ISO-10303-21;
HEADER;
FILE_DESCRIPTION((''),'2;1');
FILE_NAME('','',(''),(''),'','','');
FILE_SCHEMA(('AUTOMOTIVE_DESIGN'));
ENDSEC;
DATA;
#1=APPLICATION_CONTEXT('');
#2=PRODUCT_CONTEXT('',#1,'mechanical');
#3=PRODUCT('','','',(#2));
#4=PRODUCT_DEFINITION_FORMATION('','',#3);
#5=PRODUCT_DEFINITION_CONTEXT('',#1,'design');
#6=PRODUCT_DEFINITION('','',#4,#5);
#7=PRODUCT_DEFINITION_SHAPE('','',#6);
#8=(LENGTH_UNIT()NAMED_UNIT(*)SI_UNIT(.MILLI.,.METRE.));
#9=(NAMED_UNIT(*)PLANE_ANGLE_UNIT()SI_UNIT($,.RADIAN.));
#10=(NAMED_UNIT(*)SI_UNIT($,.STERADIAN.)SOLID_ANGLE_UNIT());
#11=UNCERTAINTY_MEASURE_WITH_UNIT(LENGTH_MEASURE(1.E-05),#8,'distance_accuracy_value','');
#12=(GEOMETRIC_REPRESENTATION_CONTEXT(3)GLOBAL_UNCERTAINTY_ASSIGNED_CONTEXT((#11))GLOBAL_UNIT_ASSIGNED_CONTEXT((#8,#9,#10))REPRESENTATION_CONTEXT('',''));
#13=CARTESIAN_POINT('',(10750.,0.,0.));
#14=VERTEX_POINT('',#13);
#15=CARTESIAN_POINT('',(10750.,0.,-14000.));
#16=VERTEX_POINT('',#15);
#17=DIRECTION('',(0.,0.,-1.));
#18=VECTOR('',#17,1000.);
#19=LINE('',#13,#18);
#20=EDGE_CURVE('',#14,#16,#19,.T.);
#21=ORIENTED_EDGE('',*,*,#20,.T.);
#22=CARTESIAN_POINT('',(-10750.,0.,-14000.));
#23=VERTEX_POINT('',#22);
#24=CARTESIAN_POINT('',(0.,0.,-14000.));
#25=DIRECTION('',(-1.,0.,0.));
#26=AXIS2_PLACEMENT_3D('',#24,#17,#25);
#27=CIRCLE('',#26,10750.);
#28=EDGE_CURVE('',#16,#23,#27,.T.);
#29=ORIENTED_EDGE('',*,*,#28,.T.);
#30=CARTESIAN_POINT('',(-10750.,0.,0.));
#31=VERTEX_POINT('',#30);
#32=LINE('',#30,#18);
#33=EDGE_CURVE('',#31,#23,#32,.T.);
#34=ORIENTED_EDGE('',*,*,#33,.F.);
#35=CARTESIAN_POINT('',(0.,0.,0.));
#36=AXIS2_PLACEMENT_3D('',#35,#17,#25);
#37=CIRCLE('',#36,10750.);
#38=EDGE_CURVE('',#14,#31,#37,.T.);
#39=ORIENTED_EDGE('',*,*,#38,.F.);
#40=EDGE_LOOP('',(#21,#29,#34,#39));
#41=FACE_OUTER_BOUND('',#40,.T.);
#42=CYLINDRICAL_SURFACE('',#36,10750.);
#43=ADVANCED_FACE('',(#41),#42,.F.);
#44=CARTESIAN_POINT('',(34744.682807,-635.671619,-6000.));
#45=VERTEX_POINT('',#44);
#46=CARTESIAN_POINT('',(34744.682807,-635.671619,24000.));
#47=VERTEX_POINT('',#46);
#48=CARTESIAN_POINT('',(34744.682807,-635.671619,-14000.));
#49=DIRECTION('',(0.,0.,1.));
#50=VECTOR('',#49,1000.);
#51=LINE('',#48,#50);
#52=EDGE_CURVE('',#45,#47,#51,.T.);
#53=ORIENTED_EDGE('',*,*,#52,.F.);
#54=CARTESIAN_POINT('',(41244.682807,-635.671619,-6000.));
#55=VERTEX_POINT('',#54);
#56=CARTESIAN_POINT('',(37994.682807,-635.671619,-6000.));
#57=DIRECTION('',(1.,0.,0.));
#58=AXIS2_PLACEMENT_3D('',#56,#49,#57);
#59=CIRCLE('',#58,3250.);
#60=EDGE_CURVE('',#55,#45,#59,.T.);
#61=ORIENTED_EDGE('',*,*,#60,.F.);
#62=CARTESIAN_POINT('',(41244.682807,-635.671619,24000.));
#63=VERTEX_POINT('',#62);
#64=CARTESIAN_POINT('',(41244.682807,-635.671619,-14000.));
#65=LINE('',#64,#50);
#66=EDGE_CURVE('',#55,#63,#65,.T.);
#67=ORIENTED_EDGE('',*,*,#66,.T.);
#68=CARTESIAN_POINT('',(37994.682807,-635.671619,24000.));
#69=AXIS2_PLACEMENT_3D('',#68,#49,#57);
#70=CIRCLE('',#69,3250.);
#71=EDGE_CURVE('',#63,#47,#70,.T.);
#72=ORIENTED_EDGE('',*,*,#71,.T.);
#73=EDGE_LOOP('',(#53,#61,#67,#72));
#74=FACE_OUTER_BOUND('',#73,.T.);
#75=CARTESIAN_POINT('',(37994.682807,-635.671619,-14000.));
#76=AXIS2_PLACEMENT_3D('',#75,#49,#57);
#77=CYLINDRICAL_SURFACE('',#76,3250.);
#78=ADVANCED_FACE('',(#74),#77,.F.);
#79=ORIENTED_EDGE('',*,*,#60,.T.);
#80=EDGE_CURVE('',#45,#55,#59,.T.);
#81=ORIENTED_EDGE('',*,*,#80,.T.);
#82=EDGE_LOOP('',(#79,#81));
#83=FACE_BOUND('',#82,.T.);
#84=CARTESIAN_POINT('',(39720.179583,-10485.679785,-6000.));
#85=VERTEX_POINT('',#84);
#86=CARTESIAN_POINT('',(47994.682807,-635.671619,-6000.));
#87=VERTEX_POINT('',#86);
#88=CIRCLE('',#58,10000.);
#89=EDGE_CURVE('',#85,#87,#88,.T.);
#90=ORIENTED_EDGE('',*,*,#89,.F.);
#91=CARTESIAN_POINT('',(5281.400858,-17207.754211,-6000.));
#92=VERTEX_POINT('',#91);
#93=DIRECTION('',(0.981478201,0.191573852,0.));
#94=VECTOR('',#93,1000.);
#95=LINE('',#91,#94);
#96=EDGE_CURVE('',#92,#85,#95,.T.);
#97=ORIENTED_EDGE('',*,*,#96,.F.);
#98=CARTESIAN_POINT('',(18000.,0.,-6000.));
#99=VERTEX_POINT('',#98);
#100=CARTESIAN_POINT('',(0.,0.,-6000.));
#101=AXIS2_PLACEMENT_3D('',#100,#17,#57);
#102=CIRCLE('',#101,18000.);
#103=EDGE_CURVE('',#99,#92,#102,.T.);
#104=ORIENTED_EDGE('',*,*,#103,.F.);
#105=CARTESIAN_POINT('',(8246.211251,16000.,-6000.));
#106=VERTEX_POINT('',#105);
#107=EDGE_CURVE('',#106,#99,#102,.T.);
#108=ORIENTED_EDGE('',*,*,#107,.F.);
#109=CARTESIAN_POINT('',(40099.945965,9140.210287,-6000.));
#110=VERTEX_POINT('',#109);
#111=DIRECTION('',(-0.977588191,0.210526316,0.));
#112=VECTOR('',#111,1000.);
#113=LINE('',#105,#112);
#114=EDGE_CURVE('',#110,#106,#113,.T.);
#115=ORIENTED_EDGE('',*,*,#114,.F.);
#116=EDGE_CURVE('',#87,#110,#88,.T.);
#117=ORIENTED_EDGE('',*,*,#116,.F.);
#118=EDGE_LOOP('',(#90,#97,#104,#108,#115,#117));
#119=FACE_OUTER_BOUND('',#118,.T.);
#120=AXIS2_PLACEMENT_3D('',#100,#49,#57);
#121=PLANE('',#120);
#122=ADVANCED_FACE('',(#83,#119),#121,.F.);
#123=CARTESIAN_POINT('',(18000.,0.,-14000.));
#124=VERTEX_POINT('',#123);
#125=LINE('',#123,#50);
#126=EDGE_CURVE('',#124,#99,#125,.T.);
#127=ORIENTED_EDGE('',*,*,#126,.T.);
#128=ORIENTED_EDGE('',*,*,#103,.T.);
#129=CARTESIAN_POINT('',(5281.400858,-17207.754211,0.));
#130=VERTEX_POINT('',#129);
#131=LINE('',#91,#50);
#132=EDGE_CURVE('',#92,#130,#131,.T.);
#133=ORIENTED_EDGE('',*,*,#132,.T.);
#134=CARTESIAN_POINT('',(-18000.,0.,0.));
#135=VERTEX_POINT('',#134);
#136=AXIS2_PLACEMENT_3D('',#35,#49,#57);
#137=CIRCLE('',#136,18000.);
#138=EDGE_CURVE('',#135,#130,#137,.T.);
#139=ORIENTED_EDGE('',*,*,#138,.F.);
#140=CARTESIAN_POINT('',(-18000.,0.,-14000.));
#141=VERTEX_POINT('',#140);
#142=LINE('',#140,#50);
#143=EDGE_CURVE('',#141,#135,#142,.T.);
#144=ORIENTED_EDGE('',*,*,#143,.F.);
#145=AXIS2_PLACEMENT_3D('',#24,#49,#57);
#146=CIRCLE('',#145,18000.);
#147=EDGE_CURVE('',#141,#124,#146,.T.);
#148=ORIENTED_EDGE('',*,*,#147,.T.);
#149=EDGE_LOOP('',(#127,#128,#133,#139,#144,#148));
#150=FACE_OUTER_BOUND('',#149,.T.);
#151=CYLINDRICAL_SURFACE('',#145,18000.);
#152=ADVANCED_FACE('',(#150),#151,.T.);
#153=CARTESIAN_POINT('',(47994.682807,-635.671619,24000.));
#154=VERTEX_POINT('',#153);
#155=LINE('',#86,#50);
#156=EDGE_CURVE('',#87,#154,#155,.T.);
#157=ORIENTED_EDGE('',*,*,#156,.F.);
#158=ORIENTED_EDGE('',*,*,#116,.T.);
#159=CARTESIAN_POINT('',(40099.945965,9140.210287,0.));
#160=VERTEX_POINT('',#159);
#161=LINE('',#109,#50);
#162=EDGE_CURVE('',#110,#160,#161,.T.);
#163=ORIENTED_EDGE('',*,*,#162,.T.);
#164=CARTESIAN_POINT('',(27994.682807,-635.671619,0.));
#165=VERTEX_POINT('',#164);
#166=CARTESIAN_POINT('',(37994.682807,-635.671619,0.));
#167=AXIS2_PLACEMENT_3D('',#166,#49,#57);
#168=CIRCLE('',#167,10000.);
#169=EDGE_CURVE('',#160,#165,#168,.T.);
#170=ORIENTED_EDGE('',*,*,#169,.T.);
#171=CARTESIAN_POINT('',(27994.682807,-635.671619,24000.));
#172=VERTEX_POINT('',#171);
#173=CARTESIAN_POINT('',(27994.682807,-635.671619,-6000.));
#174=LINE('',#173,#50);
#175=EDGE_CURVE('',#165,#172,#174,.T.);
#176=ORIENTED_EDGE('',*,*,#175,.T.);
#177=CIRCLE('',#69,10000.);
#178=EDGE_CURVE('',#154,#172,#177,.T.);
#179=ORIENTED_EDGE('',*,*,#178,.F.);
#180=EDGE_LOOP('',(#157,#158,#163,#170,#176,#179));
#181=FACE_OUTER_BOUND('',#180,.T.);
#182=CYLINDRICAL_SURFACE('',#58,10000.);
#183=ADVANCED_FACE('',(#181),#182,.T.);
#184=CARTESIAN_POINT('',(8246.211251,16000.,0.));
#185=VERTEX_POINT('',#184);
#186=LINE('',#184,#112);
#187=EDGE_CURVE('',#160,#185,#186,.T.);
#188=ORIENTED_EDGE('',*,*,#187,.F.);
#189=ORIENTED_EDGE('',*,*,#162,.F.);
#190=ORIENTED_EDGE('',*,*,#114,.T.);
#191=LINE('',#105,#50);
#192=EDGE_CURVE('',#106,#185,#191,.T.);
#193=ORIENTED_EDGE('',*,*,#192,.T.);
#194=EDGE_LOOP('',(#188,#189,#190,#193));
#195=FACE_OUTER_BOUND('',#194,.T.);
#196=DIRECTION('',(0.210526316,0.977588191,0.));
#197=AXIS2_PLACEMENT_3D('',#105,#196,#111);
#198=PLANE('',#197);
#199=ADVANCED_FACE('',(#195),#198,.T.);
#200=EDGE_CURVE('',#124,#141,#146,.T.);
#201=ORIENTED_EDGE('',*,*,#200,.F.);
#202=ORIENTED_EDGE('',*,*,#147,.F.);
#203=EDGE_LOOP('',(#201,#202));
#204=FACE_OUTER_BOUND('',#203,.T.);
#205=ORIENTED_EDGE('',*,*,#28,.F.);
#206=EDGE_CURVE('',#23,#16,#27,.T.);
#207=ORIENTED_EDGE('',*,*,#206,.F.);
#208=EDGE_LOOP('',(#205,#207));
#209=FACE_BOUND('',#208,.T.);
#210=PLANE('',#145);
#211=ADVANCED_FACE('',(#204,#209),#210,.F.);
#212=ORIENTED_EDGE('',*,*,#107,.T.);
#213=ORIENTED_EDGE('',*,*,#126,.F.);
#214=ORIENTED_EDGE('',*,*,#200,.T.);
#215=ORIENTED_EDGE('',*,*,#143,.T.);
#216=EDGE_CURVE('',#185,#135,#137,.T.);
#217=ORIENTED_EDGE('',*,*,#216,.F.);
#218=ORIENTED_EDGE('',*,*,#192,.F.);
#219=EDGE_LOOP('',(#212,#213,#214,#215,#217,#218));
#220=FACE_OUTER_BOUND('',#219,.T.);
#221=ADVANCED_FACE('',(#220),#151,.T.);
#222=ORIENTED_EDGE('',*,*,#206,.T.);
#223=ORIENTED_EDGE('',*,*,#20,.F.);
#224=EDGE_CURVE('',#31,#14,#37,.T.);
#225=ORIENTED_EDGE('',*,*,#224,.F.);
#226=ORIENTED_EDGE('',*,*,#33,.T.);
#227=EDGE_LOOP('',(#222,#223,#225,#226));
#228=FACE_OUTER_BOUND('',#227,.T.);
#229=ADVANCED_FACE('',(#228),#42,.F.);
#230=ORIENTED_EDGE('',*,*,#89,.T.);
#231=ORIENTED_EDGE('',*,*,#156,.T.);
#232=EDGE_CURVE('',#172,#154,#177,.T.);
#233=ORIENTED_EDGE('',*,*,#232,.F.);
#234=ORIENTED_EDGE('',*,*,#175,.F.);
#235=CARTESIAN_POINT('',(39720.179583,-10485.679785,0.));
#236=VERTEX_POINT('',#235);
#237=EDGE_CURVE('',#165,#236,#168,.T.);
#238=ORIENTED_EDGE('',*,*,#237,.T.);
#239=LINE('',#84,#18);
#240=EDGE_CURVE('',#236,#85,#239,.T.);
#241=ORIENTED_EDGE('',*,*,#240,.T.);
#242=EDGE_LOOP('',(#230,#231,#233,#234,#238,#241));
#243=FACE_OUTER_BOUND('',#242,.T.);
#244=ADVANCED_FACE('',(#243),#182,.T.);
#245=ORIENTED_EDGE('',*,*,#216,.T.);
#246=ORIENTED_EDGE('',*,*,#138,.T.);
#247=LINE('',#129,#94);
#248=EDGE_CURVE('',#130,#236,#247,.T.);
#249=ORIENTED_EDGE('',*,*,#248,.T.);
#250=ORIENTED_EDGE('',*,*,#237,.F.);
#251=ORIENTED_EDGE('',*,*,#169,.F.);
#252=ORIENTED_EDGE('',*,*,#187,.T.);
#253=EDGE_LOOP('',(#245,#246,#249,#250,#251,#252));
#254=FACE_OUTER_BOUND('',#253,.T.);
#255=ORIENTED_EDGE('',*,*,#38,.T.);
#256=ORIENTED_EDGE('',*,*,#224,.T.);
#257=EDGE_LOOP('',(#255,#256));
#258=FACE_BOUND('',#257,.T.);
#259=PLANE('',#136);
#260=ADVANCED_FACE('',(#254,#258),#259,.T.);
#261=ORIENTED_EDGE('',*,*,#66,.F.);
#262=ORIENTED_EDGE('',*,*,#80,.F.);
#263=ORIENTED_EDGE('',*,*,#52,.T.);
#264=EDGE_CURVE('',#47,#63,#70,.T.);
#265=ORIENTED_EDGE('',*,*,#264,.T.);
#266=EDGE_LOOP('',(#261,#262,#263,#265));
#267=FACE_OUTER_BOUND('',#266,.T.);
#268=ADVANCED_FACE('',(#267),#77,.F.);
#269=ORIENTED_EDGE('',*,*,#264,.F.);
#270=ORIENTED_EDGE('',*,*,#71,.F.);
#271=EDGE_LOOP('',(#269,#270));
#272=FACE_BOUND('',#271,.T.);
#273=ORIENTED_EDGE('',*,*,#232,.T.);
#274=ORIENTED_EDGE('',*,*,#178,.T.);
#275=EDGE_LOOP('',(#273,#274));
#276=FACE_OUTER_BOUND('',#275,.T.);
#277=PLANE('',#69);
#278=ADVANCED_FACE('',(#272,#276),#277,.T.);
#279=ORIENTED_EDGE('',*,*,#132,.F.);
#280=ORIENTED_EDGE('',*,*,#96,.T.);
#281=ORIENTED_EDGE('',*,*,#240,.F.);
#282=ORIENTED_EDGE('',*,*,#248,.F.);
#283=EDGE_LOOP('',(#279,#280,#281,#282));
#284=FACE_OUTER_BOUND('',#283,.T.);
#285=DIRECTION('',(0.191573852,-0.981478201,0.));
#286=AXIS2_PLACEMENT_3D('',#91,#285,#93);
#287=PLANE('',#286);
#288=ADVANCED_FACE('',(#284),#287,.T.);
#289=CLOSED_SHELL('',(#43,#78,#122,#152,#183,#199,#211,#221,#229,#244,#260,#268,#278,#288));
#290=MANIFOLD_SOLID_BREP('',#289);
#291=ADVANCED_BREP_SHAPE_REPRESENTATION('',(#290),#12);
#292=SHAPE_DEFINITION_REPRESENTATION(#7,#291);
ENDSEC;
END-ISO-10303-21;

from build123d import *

# Parameters (mm, degrees)
MAIN_HUB_SKETCH_R      = 18000
MAIN_HUB_36_DEPTH      = 14000
HUB_BORE_SKETCH_R      = 10750
HUB_BORE_21_5_DEPTH    = 14000
ARM_WEB_DEPTH          = 6000
PIN_BOSS_20_DEPTH      = 24000
PIN_BOSS_20_DEPTH_BACK = 6000
PIN_BOSS_SKETCH_R      = 10000
PIN_HOLE_SKETCH_R      = 3250
PIN_HOLE_6_5_DEPTH     = 63809.225000621


with BuildPart() as part:
    # Main Hub Sketch → Main Hub Ø36 (new body)
    with BuildSketch(Plane.XY):
        Circle(MAIN_HUB_SKETCH_R)
    extrude(amount=-MAIN_HUB_36_DEPTH)

    # Hub Bore Sketch → Hub Bore Ø21.5 (cut)
    with BuildSketch(Plane(origin=(0, 0, -14000), x_dir=(-1, 0, 0), z_dir=(0, 0, -1))):
        Circle(HUB_BORE_SKETCH_R)
    extrude(amount=-HUB_BORE_21_5_DEPTH, mode=Mode.SUBTRACT)

    # Arm Web Sketch → Arm Web (add)
    with BuildSketch(Plane.XY):
        with BuildLine():
            Line((8246.211251235, 16000), (40099.945964742, 9140.210286914))
            ThreePointArc((40099.945964742, 9140.210286914), (47994.682806847, -635.671618879), (40099.945964742, -10411.553524672))
            Line((40099.945964742, -10411.553524672), (5281.400857529, -17207.754210881))
            ThreePointArc((5281.400857529, -17207.754210881), (17928.686713585, -1600.685080249), (8246.211251235, 16000))
        make_face()
    extrude(amount=-ARM_WEB_DEPTH)

    # Pin Boss Sketch → Pin Boss Ø20 (add, two sides: drawn at the far end of the back side and taken through both)
    with BuildSketch(Plane.XY.offset(-PIN_BOSS_20_DEPTH_BACK)):
        with Locations((37994.682806847, -635.671618879)):
            Circle(PIN_BOSS_SKETCH_R)
    extrude(amount=PIN_BOSS_20_DEPTH + PIN_BOSS_20_DEPTH_BACK)

    # Pin Hole Sketch → Pin Hole Ø6.5 (cut, through all)
    with BuildSketch(Plane.XY.offset(24000)):
        with Locations((37994.682806847, -635.671618879)):
            Circle(PIN_HOLE_SKETCH_R)
    extrude(amount=-PIN_HOLE_6_5_DEPTH, mode=Mode.SUBTRACT)


solid = part.part
